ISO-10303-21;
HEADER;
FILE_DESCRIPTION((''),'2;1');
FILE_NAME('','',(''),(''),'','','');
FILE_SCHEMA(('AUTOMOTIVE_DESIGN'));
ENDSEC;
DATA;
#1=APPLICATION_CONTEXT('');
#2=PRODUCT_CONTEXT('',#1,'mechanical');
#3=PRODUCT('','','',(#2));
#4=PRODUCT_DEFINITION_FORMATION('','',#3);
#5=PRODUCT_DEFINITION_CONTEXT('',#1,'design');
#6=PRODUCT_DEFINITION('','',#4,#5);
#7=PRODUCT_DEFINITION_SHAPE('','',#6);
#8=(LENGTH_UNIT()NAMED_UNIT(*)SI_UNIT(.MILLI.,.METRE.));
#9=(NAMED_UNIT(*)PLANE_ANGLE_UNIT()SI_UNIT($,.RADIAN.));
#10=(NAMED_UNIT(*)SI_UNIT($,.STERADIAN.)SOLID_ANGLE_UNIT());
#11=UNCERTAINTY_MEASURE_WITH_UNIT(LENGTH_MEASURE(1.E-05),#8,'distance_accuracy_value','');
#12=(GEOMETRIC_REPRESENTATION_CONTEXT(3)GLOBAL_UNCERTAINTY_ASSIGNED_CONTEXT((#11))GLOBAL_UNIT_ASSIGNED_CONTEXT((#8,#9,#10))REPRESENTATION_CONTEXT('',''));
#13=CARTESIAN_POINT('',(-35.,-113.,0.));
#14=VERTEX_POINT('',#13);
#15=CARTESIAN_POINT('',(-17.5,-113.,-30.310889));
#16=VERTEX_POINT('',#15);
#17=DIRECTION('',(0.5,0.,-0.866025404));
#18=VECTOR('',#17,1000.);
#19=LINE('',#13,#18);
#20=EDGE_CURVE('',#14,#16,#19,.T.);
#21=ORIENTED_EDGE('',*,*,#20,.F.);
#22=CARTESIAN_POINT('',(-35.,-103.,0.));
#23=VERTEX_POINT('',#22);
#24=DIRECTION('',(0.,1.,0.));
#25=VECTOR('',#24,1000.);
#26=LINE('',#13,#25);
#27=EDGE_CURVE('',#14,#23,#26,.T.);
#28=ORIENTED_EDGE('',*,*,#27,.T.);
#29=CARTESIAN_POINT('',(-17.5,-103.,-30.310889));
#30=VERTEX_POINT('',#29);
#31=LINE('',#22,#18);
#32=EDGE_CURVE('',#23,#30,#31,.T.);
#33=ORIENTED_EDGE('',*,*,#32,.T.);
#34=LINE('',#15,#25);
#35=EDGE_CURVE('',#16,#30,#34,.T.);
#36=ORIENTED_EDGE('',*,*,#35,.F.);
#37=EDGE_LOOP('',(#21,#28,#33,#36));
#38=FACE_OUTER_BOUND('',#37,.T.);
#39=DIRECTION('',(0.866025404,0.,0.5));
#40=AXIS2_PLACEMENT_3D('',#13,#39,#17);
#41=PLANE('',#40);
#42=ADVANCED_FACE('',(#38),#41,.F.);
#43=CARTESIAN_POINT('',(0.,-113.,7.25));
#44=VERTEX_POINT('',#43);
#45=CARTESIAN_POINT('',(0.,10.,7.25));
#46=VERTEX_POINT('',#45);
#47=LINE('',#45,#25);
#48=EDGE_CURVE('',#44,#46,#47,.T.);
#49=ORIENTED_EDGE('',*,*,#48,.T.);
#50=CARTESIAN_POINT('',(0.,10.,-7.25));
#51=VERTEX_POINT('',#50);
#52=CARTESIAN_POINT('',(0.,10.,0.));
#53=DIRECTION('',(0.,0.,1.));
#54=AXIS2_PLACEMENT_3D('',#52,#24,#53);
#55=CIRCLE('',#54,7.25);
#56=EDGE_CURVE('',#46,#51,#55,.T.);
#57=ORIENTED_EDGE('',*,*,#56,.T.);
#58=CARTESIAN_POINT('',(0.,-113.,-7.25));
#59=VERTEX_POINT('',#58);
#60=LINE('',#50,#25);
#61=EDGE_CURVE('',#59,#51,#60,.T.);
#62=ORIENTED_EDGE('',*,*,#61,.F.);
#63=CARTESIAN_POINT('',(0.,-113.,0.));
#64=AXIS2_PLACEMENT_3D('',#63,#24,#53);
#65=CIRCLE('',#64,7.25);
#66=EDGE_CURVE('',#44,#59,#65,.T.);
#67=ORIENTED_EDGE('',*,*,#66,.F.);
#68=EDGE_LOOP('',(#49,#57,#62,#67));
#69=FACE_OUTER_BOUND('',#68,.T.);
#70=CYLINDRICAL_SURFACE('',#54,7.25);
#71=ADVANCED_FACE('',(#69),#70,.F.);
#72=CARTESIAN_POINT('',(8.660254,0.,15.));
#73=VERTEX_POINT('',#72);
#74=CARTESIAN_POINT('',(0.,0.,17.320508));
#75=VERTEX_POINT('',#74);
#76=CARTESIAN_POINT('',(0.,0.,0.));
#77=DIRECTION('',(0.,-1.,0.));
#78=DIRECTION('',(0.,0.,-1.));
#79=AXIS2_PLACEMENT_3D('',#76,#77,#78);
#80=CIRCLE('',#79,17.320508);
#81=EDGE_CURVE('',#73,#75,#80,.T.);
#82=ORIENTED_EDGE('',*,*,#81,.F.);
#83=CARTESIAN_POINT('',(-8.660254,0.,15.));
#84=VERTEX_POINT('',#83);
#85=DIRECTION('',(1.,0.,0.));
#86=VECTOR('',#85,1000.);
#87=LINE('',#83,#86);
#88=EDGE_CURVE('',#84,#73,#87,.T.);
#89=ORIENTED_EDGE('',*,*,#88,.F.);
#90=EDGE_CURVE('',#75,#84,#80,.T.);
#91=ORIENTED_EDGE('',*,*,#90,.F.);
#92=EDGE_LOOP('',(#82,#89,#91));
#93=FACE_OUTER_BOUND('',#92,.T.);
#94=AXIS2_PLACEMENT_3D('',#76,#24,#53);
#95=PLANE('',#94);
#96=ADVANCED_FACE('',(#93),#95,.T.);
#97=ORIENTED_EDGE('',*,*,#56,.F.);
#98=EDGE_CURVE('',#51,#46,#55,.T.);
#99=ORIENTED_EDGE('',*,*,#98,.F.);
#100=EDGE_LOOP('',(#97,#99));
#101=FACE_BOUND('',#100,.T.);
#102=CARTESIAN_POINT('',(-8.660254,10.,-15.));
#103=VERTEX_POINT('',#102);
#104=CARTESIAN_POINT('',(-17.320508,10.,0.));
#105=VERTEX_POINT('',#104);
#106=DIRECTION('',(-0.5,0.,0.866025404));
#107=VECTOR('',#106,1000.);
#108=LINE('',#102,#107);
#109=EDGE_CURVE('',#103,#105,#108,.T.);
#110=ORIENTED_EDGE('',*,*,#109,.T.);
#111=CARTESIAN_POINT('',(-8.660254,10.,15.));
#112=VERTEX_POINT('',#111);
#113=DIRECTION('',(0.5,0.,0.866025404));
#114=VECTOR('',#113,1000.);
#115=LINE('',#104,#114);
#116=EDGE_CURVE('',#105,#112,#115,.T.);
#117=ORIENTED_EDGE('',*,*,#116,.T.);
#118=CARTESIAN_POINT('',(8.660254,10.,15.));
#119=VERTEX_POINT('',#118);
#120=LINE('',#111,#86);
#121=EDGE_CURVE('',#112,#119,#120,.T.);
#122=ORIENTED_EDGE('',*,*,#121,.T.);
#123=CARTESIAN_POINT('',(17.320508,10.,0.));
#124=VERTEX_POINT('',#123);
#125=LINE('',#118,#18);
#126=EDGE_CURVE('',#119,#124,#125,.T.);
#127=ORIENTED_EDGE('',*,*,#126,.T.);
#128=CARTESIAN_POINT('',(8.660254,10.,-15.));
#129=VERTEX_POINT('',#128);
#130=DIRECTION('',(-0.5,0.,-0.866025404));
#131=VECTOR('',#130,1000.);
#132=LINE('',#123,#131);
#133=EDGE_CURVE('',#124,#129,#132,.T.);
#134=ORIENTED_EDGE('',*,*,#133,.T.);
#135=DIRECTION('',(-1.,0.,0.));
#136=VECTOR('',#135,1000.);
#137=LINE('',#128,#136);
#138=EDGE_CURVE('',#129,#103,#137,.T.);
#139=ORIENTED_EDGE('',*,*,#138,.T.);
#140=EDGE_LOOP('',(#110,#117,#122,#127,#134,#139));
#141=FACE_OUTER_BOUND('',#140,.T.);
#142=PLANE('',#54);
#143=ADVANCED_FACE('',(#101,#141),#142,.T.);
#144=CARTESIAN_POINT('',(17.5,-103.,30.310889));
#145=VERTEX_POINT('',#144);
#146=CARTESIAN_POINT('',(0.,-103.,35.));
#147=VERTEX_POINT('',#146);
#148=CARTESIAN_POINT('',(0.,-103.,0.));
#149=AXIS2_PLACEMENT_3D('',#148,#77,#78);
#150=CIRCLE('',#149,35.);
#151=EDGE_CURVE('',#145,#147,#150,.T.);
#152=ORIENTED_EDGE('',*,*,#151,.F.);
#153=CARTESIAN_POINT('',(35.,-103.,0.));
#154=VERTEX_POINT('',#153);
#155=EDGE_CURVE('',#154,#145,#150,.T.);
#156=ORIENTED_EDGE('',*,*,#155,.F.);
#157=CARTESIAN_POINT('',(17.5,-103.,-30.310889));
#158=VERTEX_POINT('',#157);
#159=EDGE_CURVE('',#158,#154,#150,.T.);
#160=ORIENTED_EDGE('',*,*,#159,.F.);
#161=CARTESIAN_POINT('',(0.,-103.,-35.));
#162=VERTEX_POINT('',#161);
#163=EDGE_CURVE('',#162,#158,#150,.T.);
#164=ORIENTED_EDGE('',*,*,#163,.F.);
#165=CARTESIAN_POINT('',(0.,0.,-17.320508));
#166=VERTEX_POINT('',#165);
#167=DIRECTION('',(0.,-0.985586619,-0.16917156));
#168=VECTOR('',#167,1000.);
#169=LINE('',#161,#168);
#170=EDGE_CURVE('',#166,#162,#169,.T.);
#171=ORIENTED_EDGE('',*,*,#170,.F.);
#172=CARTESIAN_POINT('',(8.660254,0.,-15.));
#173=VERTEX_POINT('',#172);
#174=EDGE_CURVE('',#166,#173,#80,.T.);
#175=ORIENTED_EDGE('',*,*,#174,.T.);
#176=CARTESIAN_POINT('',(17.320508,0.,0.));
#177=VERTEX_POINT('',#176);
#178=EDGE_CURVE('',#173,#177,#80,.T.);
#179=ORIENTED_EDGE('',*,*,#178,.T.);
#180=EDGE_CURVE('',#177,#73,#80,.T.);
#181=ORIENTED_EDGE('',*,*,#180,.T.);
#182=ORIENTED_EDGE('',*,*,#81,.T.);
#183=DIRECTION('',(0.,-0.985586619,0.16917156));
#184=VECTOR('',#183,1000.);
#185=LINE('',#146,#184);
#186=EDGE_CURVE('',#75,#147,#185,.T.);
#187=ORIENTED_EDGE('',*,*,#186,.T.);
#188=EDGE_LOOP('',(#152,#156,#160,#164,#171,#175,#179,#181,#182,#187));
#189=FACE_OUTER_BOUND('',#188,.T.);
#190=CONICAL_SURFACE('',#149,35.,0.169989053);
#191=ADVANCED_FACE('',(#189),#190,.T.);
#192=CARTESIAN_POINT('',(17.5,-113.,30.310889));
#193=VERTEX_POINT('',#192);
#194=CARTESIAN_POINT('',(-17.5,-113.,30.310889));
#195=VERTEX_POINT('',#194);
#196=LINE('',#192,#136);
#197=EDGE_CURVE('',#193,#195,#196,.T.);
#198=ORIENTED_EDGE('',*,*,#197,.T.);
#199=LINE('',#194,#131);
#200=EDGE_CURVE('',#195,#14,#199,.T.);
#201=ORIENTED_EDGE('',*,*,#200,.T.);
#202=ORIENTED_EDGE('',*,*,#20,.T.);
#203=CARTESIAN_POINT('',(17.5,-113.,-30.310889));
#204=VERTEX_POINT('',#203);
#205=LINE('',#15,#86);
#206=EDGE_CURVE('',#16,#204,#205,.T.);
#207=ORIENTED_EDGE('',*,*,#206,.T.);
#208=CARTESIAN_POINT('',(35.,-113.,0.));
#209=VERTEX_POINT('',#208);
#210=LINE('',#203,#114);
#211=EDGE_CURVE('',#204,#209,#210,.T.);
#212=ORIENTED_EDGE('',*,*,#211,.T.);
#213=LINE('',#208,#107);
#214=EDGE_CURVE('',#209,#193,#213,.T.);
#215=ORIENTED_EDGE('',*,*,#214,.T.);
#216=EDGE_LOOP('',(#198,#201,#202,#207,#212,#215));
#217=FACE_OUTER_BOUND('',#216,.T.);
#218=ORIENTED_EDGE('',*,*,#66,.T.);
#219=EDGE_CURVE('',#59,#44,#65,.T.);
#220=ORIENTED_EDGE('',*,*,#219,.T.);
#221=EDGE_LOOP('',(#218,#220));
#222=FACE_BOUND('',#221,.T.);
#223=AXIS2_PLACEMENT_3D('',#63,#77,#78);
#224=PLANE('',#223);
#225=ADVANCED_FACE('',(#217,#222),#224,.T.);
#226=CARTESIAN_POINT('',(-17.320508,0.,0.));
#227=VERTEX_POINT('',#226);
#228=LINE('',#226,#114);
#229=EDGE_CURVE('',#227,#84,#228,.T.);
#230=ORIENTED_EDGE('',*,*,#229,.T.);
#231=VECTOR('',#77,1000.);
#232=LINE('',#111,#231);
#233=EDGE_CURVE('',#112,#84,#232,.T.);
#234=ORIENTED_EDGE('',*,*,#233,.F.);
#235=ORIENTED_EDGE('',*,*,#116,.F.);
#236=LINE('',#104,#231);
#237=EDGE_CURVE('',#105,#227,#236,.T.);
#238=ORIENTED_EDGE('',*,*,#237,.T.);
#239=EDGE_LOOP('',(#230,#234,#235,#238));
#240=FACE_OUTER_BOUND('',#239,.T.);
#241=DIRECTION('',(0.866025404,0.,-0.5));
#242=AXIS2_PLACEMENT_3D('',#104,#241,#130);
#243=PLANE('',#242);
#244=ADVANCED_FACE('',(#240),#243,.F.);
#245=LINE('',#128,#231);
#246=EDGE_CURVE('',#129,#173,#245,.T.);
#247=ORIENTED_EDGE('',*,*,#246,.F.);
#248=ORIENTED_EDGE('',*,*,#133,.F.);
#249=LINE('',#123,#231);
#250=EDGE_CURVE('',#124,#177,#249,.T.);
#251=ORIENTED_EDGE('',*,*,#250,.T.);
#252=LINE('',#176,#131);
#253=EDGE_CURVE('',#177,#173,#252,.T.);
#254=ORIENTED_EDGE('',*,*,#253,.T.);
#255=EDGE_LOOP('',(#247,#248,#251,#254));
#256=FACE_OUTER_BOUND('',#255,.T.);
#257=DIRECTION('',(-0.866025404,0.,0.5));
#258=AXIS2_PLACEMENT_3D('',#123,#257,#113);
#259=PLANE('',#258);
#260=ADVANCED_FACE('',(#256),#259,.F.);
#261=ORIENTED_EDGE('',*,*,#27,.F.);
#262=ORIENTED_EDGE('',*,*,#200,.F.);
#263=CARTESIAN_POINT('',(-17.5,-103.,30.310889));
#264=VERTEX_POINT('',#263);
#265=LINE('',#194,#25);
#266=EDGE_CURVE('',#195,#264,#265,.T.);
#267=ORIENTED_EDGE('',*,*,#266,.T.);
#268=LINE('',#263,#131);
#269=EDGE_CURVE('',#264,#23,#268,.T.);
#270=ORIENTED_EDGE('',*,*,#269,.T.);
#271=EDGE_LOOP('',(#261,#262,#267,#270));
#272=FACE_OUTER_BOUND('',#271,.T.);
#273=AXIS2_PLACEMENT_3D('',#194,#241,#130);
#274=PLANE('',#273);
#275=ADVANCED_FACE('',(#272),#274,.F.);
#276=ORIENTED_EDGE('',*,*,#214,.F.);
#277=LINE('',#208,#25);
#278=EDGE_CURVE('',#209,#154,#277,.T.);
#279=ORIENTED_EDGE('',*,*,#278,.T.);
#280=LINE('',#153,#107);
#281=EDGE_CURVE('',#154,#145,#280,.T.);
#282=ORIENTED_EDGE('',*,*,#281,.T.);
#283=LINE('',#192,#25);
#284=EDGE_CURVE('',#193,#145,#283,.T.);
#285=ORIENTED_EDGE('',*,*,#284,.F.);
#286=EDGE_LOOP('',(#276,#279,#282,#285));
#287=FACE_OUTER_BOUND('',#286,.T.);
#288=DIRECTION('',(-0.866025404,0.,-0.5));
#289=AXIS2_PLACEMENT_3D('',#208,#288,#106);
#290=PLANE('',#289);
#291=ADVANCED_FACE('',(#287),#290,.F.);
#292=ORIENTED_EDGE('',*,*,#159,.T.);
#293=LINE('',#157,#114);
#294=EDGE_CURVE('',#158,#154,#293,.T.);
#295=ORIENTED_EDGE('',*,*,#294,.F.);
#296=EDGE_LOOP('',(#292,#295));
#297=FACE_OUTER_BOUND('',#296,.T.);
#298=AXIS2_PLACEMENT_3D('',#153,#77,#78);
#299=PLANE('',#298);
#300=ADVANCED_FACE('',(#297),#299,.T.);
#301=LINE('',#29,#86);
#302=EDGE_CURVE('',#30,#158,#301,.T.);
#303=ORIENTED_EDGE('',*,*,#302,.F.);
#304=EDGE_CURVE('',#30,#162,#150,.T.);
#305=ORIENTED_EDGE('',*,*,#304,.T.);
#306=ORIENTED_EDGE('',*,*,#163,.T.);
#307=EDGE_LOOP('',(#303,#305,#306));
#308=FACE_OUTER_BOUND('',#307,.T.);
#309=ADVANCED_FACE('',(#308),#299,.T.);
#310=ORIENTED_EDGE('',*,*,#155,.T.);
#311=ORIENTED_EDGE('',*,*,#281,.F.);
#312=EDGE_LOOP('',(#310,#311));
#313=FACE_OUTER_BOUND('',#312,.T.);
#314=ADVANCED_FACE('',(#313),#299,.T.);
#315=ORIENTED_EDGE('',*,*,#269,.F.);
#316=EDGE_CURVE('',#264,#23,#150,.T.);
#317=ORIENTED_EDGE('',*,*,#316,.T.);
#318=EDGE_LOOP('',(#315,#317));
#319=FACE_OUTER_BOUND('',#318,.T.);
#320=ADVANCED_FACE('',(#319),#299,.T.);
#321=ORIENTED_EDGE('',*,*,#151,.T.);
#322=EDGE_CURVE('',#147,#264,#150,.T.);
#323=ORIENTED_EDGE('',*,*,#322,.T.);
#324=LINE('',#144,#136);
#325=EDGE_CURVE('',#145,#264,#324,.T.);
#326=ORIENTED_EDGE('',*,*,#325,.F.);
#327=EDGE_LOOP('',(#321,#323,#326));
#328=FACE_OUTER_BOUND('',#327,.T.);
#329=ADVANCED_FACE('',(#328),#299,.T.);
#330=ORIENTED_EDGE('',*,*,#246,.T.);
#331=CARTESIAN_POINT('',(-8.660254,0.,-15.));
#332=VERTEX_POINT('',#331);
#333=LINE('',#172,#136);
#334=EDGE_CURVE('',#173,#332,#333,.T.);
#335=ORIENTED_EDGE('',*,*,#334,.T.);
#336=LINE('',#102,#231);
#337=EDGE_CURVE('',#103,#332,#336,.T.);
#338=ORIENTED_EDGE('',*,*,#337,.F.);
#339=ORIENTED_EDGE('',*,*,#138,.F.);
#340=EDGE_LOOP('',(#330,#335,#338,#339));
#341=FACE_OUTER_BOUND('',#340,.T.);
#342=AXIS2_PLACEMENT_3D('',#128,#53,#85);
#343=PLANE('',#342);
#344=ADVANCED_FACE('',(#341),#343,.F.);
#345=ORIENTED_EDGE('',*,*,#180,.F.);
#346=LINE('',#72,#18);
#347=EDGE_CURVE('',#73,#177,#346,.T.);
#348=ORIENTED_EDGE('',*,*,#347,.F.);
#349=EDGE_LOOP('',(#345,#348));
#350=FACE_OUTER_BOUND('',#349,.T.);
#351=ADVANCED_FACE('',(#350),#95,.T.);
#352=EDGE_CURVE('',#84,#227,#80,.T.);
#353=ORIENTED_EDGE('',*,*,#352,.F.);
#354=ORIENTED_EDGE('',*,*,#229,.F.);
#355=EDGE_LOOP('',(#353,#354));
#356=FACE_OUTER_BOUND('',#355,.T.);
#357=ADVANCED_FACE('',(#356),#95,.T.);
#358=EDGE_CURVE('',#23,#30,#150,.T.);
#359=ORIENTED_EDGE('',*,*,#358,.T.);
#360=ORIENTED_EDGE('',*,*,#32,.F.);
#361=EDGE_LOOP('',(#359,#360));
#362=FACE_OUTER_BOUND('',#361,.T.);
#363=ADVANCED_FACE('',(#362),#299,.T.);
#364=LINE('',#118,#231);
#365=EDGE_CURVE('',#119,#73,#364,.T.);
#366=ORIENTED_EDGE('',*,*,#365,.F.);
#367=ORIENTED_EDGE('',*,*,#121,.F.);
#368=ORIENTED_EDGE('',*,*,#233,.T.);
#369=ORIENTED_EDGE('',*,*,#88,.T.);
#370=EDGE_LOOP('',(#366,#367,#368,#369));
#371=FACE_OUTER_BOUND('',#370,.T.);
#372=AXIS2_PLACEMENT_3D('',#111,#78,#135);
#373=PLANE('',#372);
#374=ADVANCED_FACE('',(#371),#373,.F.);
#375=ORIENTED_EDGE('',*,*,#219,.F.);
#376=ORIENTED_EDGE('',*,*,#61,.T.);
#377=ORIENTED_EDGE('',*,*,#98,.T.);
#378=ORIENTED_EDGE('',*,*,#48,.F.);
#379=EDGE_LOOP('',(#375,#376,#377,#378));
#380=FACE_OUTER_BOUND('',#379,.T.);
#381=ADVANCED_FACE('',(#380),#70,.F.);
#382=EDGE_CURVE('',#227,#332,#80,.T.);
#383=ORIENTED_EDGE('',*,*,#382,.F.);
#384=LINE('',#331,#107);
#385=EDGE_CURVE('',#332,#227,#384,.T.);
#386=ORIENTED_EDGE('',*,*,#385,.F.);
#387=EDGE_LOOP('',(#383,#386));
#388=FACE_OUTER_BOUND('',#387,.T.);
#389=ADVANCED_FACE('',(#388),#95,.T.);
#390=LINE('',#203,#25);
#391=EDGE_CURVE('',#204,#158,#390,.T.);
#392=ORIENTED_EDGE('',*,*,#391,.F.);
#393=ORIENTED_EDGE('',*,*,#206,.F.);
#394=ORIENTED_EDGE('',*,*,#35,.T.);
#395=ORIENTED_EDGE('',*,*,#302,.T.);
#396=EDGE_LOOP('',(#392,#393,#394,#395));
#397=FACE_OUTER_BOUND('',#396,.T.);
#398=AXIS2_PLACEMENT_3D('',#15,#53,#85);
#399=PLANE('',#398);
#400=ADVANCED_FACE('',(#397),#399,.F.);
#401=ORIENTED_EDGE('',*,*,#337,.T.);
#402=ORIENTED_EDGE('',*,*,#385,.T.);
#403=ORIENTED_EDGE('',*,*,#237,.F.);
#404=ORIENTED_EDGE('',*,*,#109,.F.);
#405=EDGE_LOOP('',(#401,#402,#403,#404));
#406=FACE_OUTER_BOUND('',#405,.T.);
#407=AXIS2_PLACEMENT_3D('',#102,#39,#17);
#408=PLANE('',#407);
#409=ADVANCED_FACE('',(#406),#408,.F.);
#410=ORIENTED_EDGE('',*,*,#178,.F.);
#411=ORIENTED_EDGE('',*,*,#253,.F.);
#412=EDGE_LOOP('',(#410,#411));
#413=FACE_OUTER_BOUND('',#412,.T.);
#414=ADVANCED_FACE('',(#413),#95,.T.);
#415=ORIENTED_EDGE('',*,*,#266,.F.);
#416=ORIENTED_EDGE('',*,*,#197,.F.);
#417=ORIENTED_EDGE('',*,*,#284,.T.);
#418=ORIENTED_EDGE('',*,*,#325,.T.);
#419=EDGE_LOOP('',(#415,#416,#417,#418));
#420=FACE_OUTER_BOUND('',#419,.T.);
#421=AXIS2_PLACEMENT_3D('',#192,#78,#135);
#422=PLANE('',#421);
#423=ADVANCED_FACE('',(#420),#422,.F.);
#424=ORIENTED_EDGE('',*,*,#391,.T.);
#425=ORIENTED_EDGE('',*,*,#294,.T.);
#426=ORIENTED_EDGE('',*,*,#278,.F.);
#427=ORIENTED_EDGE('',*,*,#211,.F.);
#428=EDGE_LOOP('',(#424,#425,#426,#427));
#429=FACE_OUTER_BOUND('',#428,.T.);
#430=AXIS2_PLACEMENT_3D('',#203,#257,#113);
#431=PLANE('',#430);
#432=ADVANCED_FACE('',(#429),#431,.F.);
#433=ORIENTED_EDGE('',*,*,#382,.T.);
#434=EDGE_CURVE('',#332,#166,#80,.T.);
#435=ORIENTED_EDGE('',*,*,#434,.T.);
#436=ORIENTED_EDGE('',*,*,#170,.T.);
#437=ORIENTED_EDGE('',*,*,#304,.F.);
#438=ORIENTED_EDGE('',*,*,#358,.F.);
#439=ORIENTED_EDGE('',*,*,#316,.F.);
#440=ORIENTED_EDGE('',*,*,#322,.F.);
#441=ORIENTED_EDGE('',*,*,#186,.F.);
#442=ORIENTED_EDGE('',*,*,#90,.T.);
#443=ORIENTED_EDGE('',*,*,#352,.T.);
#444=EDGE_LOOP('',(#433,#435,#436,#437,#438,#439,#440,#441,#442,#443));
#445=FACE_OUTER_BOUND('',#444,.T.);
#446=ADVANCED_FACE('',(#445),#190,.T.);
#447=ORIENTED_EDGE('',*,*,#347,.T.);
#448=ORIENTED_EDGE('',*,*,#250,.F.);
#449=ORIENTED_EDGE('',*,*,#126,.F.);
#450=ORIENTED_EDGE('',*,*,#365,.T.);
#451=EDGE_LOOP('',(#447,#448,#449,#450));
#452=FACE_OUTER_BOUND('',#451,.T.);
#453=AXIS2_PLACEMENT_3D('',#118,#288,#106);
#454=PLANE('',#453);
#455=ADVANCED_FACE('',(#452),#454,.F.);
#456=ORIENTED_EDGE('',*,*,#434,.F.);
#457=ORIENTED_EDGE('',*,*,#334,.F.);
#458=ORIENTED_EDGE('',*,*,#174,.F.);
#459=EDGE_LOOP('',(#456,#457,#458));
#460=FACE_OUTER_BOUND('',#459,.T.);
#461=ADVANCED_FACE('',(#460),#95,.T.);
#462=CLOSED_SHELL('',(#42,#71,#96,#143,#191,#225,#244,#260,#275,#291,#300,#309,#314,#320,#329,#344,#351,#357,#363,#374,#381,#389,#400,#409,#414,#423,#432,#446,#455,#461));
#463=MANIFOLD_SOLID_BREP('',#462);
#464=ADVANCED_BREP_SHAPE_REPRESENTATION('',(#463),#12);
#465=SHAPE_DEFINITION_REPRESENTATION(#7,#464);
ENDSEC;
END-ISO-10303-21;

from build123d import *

# Parameters (mm, degrees)
BOSS_EXTRUDE1_DEPTH    = 10
BOSS_EXTRUDE2_DEPTH    = 10
M16X1_5_TAPPED_HOLE1_D = 14.5


with BuildPart() as part:
    # Sketch1 → Boss-Extrude1 (new body)
    with BuildSketch(Plane(origin=(0, 0, 0), x_dir=(1, 0, 0), z_dir=(0, 1, 0))):
        Polygon((8.660254038, -15), (17.320508076, 0), (8.660254038, 15), (-8.660254038, 15), (-17.320508076, 0), (-8.660254038, -15), align=None)
    extrude(amount=BOSS_EXTRUDE1_DEPTH)

    # Sketch4 → Revolve1 (revolve)
    with BuildSketch(Plane.XY, mode=Mode.PRIVATE) as revolve1_sk:
        Polygon((0, 0), (17.320508076, 0), (35, -103), (0, -103), align=None)
    revolve(revolve1_sk.sketch.rotate(Axis((0, -103, 0), (0, 1, 0)), 90), axis=Axis((0, -103, 0), (0, 1, 0)))

    # Sketch7 → Boss-Extrude2 (add)
    with BuildSketch(Plane.XZ.offset(103)):
        Polygon((17.5, 30.310889132), (-17.5, 30.310889132), (-35, 0), (-17.5, -30.310889132), (17.5, -30.310889132), (35, 0), align=None)
    extrude(amount=BOSS_EXTRUDE2_DEPTH)

    # M16x1.5 Tapped Hole1 (through all)
    with Locations(Plane(origin=(0, 10, 0), x_dir=(1, 0, 0), z_dir=(0, 1, 0))):
        with Locations((0, 0)):
            Hole(M16X1_5_TAPPED_HOLE1_D / 2)


solid = part.part
